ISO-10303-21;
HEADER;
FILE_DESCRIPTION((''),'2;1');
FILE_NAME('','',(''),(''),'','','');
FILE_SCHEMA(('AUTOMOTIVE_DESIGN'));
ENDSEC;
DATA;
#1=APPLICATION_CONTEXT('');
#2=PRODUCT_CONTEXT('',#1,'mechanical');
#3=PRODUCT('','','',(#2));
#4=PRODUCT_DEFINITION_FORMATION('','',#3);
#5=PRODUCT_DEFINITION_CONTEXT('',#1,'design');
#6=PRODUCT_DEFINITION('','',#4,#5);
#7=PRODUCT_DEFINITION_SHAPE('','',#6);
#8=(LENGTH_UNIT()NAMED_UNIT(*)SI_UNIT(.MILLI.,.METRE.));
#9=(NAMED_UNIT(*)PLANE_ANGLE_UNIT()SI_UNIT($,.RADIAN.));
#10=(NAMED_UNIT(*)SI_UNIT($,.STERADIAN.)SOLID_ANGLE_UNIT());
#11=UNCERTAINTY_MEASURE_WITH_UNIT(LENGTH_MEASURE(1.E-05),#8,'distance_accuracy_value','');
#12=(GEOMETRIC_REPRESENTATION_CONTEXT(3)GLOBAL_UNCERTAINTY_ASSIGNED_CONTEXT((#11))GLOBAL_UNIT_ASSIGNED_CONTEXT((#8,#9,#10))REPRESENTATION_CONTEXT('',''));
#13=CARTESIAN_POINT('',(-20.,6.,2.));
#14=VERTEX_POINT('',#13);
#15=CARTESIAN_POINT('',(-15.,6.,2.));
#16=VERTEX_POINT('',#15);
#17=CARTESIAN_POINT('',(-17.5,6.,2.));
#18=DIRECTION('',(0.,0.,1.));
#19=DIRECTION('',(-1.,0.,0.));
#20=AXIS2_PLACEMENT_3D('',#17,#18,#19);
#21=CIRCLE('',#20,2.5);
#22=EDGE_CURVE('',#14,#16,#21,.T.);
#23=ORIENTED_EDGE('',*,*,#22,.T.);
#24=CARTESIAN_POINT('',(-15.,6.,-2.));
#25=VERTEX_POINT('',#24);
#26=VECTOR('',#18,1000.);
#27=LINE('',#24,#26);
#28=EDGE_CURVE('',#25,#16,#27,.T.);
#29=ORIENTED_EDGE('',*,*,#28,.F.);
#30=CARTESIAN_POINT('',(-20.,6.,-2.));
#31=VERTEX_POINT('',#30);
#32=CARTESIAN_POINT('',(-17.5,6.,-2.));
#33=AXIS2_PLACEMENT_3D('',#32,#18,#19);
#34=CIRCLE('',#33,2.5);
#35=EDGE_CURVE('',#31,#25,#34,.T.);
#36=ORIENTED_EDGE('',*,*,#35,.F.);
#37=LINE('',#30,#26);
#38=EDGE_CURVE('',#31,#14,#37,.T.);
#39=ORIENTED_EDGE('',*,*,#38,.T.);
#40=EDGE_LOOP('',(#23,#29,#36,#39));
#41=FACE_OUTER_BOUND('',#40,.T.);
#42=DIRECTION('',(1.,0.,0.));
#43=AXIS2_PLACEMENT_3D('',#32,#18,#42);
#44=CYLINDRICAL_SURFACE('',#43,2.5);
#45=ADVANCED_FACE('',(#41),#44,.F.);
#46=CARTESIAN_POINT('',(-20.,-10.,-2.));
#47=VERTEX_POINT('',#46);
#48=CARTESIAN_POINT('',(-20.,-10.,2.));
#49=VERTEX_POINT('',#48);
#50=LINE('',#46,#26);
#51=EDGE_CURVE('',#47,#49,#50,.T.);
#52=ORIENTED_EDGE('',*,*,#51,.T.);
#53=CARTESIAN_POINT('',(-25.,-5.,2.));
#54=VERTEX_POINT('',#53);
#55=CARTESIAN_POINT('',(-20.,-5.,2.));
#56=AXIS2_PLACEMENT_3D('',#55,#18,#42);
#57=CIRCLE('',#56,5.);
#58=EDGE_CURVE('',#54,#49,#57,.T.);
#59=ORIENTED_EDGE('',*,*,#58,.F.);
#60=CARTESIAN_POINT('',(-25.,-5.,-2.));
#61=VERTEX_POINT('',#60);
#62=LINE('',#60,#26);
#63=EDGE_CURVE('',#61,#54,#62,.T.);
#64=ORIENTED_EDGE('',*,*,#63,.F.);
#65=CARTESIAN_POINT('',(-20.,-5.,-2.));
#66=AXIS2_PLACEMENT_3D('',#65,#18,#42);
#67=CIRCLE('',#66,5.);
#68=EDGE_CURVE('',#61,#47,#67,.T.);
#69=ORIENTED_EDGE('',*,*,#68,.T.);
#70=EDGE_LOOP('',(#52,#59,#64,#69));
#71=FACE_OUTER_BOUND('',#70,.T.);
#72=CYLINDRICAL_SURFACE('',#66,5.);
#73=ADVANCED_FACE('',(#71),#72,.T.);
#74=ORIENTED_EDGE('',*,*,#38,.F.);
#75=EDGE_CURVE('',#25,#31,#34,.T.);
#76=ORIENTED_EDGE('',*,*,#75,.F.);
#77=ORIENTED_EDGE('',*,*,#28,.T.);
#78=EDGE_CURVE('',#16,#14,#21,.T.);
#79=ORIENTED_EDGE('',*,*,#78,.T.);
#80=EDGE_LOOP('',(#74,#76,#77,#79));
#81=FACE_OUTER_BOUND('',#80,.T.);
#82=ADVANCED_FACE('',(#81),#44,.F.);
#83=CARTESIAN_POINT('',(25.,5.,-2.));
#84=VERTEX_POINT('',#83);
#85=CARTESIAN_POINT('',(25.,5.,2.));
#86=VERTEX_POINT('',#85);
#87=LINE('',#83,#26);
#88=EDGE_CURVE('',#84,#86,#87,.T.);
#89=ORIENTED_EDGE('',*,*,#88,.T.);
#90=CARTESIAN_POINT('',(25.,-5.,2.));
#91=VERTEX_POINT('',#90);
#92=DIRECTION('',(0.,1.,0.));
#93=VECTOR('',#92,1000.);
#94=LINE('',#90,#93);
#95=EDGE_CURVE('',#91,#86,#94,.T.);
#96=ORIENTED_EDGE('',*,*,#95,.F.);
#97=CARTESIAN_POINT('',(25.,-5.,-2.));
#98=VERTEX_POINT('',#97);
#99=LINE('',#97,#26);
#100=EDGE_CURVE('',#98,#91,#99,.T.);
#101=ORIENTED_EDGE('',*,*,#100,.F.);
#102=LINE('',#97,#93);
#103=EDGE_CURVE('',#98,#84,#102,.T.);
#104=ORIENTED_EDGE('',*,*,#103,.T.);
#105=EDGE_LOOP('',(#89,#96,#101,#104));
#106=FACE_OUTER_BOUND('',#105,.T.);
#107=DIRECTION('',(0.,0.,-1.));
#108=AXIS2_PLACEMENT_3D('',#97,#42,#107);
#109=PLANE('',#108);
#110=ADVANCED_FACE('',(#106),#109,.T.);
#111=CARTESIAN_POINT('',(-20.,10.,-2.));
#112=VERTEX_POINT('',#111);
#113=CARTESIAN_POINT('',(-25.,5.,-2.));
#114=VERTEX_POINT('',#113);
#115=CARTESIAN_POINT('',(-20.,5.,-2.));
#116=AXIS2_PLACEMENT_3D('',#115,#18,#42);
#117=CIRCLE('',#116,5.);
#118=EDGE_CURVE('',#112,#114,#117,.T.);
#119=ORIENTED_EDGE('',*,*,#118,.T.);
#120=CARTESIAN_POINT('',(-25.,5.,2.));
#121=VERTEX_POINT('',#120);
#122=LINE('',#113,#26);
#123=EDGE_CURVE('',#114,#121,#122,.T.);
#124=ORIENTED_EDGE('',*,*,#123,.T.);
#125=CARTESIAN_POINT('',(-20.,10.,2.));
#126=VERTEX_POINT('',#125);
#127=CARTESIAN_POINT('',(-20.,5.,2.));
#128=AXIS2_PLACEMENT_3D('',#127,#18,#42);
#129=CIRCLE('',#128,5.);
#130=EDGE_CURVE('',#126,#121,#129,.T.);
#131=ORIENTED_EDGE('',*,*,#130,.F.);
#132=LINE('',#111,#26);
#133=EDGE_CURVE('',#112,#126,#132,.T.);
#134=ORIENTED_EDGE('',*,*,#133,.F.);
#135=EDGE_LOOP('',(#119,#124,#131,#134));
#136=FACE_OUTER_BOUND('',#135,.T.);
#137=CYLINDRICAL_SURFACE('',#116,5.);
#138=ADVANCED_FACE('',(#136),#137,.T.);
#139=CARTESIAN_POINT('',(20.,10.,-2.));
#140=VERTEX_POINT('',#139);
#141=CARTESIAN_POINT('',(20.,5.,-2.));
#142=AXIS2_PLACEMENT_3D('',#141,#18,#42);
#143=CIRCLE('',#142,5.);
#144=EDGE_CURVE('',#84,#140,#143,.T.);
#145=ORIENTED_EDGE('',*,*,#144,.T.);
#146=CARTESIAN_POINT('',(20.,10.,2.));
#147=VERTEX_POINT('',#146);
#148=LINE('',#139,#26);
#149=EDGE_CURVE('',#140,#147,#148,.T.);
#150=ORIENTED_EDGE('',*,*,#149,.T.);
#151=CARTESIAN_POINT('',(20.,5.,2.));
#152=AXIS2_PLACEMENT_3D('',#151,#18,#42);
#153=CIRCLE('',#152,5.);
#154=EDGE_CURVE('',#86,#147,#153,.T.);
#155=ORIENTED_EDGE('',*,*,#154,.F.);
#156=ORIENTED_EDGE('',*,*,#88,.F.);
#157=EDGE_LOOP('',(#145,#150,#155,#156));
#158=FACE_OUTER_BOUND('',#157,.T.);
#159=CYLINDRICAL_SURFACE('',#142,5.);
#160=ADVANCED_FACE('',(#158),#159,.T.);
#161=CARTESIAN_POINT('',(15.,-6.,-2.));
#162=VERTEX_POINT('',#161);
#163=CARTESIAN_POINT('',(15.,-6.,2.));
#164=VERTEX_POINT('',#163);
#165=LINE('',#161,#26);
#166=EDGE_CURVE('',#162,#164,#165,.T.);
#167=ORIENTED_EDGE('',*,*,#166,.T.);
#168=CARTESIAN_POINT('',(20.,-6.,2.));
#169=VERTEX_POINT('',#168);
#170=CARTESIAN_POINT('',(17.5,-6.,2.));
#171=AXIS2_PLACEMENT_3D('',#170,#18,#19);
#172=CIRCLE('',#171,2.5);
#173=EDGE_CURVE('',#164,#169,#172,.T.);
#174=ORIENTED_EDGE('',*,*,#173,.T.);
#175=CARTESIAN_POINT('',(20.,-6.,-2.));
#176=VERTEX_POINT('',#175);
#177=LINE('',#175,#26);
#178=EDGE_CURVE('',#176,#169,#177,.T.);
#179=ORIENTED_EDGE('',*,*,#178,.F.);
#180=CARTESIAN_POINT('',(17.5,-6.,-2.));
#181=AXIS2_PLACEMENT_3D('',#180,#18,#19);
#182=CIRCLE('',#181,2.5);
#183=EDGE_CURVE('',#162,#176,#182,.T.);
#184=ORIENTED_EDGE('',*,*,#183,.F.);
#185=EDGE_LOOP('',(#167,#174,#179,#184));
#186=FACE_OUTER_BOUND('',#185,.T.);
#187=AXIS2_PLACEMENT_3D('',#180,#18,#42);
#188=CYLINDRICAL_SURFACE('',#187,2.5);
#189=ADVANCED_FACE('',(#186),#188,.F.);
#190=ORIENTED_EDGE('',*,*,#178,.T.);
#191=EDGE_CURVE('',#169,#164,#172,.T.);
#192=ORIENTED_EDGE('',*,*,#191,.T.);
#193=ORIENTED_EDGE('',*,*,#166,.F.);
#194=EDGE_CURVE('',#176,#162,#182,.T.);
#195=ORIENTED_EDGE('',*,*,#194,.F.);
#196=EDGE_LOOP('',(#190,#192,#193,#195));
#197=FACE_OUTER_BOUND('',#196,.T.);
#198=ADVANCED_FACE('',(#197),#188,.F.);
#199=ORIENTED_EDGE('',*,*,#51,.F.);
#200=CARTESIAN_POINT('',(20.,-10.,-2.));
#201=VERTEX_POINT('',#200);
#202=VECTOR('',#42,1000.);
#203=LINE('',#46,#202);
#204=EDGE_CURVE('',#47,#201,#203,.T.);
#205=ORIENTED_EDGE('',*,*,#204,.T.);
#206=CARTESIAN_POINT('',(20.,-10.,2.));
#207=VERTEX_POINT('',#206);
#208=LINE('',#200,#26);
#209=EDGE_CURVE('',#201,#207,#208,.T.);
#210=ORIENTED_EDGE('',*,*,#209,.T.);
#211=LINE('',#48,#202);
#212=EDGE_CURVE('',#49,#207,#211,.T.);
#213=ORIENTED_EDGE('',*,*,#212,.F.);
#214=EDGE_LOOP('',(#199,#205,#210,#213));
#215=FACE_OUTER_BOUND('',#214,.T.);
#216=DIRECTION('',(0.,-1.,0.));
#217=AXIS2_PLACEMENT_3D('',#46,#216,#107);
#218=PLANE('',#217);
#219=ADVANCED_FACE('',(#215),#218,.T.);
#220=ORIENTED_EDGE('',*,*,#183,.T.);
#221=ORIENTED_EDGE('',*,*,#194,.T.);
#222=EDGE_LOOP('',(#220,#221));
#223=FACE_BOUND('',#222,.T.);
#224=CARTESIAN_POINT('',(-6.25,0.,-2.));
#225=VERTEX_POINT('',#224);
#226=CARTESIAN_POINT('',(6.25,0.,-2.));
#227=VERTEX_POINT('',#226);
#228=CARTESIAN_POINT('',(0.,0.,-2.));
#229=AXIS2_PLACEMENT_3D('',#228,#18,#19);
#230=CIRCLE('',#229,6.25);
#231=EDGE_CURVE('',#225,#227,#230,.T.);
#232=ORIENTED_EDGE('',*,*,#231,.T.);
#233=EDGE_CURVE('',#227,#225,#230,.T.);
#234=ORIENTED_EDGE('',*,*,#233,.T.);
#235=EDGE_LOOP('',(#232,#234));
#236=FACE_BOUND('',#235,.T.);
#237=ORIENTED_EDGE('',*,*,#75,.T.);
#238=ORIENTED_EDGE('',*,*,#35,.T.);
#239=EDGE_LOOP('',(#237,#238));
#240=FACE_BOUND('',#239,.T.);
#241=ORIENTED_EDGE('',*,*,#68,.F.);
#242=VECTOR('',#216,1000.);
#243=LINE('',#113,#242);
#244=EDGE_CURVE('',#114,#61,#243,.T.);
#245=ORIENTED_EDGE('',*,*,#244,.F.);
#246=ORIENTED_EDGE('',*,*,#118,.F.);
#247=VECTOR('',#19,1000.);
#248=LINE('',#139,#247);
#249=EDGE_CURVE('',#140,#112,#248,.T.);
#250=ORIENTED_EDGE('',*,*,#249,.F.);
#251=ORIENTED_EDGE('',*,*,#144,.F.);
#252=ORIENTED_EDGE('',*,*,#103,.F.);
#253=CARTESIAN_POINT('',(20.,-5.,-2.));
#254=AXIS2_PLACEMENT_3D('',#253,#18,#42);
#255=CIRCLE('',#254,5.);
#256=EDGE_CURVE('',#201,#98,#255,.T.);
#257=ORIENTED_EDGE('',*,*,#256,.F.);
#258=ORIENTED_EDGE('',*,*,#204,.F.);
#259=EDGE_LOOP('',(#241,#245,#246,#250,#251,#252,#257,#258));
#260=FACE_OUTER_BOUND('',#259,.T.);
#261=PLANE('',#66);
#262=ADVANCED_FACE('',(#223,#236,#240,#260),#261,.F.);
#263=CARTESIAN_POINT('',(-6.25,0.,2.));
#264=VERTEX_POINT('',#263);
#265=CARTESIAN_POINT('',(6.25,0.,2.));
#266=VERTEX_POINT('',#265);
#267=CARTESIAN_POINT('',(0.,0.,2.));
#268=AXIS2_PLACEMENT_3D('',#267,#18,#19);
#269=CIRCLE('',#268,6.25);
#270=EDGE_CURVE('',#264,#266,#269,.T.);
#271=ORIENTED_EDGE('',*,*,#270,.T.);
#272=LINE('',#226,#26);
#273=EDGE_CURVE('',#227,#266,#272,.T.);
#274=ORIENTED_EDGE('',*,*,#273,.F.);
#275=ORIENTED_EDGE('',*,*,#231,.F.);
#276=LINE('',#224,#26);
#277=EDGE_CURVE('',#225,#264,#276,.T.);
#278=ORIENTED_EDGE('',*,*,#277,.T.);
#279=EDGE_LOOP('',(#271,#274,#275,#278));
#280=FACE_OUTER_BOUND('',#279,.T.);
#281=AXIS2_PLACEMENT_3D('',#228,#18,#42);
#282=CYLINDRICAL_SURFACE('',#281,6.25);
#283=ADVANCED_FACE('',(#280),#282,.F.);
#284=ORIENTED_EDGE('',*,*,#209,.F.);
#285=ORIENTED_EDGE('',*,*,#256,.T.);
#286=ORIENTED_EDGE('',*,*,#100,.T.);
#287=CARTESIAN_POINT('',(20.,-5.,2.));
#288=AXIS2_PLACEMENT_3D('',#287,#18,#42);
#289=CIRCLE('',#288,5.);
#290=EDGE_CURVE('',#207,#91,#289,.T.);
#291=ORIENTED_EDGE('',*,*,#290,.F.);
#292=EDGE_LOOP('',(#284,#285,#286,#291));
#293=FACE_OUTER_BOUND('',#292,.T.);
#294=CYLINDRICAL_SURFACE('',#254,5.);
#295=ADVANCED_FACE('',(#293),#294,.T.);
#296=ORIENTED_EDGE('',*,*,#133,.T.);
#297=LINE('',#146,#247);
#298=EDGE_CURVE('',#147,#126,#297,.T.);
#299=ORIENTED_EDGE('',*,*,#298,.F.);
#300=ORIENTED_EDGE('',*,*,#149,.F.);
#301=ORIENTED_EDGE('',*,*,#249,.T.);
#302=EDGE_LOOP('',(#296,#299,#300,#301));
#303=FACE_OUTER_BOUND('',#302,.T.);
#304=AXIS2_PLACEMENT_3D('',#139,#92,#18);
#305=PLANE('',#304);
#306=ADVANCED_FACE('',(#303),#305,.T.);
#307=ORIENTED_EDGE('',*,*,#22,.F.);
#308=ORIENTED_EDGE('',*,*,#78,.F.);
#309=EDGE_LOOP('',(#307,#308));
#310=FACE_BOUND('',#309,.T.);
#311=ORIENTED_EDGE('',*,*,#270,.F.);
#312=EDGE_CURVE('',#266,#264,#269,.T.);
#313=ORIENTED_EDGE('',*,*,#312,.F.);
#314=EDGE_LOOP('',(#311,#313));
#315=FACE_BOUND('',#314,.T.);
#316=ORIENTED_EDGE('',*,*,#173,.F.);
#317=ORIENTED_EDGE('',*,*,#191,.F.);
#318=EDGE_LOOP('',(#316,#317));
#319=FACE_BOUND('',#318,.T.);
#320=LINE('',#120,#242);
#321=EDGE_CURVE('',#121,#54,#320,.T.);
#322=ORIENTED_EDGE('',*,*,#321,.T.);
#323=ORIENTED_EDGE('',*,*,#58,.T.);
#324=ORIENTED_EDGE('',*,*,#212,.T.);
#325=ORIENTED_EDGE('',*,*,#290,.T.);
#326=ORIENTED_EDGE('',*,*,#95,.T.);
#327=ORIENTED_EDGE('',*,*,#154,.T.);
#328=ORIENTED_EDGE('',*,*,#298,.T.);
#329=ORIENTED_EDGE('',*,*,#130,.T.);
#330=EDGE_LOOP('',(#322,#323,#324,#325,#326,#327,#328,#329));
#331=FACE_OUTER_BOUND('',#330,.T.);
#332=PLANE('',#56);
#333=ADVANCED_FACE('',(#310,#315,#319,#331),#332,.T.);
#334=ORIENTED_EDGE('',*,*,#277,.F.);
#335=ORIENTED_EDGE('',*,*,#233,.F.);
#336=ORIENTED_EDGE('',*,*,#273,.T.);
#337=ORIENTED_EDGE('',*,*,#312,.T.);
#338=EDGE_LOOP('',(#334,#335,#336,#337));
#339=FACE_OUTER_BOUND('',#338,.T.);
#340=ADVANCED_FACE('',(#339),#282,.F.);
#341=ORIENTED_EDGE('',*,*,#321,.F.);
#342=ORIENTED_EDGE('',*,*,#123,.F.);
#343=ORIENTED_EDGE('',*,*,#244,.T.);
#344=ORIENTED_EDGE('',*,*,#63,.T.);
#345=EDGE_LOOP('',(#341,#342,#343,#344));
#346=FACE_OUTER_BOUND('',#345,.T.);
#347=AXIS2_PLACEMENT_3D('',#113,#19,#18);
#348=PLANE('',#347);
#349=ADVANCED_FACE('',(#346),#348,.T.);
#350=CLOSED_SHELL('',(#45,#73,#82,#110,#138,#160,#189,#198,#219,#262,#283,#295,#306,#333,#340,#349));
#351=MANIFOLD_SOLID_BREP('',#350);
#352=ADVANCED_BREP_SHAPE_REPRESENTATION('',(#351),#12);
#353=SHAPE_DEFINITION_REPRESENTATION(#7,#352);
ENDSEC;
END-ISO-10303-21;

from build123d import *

# Parameters (mm, degrees)
SKETCH_1_R      = 2.5
SKETCH_1_R_2    = 6.25
EXTRUDE_1_DEPTH = 4


with BuildPart() as part:
    # 草图1 → 凸台-拉伸1 (new body)
    with BuildSketch(Plane.XY.offset(2)):
        with BuildLine():
            Line((-20, -10), (20, -10))
            ThreePointArc((20, -10), (23.535533906, -8.535533906), (25, -5))
            Line((25, -5), (25, 5))
            ThreePointArc((25, 5), (23.535533906, 8.535533906), (20, 10))
            Line((20, 10), (-20, 10))
            ThreePointArc((-20, 10), (-23.535533906, 8.535533906), (-25, 5))
            Line((-25, 5), (-25, -5))
            ThreePointArc((-25, -5), (-23.535533906, -8.535533906), (-20, -10))
        make_face()
        with Locations(Location((-17.5, 6, 0), (0, 0, 180))):
            Circle(SKETCH_1_R, mode=Mode.SUBTRACT)
        with Locations(Location((17.5, -6, 0), (0, 0, 180))):
            Circle(SKETCH_1_R, mode=Mode.SUBTRACT)
        with Locations(Location((0, 0, 0), (0, 0, 180))):
            Circle(SKETCH_1_R_2, mode=Mode.SUBTRACT)
    extrude(amount=-EXTRUDE_1_DEPTH)


solid = part.part
